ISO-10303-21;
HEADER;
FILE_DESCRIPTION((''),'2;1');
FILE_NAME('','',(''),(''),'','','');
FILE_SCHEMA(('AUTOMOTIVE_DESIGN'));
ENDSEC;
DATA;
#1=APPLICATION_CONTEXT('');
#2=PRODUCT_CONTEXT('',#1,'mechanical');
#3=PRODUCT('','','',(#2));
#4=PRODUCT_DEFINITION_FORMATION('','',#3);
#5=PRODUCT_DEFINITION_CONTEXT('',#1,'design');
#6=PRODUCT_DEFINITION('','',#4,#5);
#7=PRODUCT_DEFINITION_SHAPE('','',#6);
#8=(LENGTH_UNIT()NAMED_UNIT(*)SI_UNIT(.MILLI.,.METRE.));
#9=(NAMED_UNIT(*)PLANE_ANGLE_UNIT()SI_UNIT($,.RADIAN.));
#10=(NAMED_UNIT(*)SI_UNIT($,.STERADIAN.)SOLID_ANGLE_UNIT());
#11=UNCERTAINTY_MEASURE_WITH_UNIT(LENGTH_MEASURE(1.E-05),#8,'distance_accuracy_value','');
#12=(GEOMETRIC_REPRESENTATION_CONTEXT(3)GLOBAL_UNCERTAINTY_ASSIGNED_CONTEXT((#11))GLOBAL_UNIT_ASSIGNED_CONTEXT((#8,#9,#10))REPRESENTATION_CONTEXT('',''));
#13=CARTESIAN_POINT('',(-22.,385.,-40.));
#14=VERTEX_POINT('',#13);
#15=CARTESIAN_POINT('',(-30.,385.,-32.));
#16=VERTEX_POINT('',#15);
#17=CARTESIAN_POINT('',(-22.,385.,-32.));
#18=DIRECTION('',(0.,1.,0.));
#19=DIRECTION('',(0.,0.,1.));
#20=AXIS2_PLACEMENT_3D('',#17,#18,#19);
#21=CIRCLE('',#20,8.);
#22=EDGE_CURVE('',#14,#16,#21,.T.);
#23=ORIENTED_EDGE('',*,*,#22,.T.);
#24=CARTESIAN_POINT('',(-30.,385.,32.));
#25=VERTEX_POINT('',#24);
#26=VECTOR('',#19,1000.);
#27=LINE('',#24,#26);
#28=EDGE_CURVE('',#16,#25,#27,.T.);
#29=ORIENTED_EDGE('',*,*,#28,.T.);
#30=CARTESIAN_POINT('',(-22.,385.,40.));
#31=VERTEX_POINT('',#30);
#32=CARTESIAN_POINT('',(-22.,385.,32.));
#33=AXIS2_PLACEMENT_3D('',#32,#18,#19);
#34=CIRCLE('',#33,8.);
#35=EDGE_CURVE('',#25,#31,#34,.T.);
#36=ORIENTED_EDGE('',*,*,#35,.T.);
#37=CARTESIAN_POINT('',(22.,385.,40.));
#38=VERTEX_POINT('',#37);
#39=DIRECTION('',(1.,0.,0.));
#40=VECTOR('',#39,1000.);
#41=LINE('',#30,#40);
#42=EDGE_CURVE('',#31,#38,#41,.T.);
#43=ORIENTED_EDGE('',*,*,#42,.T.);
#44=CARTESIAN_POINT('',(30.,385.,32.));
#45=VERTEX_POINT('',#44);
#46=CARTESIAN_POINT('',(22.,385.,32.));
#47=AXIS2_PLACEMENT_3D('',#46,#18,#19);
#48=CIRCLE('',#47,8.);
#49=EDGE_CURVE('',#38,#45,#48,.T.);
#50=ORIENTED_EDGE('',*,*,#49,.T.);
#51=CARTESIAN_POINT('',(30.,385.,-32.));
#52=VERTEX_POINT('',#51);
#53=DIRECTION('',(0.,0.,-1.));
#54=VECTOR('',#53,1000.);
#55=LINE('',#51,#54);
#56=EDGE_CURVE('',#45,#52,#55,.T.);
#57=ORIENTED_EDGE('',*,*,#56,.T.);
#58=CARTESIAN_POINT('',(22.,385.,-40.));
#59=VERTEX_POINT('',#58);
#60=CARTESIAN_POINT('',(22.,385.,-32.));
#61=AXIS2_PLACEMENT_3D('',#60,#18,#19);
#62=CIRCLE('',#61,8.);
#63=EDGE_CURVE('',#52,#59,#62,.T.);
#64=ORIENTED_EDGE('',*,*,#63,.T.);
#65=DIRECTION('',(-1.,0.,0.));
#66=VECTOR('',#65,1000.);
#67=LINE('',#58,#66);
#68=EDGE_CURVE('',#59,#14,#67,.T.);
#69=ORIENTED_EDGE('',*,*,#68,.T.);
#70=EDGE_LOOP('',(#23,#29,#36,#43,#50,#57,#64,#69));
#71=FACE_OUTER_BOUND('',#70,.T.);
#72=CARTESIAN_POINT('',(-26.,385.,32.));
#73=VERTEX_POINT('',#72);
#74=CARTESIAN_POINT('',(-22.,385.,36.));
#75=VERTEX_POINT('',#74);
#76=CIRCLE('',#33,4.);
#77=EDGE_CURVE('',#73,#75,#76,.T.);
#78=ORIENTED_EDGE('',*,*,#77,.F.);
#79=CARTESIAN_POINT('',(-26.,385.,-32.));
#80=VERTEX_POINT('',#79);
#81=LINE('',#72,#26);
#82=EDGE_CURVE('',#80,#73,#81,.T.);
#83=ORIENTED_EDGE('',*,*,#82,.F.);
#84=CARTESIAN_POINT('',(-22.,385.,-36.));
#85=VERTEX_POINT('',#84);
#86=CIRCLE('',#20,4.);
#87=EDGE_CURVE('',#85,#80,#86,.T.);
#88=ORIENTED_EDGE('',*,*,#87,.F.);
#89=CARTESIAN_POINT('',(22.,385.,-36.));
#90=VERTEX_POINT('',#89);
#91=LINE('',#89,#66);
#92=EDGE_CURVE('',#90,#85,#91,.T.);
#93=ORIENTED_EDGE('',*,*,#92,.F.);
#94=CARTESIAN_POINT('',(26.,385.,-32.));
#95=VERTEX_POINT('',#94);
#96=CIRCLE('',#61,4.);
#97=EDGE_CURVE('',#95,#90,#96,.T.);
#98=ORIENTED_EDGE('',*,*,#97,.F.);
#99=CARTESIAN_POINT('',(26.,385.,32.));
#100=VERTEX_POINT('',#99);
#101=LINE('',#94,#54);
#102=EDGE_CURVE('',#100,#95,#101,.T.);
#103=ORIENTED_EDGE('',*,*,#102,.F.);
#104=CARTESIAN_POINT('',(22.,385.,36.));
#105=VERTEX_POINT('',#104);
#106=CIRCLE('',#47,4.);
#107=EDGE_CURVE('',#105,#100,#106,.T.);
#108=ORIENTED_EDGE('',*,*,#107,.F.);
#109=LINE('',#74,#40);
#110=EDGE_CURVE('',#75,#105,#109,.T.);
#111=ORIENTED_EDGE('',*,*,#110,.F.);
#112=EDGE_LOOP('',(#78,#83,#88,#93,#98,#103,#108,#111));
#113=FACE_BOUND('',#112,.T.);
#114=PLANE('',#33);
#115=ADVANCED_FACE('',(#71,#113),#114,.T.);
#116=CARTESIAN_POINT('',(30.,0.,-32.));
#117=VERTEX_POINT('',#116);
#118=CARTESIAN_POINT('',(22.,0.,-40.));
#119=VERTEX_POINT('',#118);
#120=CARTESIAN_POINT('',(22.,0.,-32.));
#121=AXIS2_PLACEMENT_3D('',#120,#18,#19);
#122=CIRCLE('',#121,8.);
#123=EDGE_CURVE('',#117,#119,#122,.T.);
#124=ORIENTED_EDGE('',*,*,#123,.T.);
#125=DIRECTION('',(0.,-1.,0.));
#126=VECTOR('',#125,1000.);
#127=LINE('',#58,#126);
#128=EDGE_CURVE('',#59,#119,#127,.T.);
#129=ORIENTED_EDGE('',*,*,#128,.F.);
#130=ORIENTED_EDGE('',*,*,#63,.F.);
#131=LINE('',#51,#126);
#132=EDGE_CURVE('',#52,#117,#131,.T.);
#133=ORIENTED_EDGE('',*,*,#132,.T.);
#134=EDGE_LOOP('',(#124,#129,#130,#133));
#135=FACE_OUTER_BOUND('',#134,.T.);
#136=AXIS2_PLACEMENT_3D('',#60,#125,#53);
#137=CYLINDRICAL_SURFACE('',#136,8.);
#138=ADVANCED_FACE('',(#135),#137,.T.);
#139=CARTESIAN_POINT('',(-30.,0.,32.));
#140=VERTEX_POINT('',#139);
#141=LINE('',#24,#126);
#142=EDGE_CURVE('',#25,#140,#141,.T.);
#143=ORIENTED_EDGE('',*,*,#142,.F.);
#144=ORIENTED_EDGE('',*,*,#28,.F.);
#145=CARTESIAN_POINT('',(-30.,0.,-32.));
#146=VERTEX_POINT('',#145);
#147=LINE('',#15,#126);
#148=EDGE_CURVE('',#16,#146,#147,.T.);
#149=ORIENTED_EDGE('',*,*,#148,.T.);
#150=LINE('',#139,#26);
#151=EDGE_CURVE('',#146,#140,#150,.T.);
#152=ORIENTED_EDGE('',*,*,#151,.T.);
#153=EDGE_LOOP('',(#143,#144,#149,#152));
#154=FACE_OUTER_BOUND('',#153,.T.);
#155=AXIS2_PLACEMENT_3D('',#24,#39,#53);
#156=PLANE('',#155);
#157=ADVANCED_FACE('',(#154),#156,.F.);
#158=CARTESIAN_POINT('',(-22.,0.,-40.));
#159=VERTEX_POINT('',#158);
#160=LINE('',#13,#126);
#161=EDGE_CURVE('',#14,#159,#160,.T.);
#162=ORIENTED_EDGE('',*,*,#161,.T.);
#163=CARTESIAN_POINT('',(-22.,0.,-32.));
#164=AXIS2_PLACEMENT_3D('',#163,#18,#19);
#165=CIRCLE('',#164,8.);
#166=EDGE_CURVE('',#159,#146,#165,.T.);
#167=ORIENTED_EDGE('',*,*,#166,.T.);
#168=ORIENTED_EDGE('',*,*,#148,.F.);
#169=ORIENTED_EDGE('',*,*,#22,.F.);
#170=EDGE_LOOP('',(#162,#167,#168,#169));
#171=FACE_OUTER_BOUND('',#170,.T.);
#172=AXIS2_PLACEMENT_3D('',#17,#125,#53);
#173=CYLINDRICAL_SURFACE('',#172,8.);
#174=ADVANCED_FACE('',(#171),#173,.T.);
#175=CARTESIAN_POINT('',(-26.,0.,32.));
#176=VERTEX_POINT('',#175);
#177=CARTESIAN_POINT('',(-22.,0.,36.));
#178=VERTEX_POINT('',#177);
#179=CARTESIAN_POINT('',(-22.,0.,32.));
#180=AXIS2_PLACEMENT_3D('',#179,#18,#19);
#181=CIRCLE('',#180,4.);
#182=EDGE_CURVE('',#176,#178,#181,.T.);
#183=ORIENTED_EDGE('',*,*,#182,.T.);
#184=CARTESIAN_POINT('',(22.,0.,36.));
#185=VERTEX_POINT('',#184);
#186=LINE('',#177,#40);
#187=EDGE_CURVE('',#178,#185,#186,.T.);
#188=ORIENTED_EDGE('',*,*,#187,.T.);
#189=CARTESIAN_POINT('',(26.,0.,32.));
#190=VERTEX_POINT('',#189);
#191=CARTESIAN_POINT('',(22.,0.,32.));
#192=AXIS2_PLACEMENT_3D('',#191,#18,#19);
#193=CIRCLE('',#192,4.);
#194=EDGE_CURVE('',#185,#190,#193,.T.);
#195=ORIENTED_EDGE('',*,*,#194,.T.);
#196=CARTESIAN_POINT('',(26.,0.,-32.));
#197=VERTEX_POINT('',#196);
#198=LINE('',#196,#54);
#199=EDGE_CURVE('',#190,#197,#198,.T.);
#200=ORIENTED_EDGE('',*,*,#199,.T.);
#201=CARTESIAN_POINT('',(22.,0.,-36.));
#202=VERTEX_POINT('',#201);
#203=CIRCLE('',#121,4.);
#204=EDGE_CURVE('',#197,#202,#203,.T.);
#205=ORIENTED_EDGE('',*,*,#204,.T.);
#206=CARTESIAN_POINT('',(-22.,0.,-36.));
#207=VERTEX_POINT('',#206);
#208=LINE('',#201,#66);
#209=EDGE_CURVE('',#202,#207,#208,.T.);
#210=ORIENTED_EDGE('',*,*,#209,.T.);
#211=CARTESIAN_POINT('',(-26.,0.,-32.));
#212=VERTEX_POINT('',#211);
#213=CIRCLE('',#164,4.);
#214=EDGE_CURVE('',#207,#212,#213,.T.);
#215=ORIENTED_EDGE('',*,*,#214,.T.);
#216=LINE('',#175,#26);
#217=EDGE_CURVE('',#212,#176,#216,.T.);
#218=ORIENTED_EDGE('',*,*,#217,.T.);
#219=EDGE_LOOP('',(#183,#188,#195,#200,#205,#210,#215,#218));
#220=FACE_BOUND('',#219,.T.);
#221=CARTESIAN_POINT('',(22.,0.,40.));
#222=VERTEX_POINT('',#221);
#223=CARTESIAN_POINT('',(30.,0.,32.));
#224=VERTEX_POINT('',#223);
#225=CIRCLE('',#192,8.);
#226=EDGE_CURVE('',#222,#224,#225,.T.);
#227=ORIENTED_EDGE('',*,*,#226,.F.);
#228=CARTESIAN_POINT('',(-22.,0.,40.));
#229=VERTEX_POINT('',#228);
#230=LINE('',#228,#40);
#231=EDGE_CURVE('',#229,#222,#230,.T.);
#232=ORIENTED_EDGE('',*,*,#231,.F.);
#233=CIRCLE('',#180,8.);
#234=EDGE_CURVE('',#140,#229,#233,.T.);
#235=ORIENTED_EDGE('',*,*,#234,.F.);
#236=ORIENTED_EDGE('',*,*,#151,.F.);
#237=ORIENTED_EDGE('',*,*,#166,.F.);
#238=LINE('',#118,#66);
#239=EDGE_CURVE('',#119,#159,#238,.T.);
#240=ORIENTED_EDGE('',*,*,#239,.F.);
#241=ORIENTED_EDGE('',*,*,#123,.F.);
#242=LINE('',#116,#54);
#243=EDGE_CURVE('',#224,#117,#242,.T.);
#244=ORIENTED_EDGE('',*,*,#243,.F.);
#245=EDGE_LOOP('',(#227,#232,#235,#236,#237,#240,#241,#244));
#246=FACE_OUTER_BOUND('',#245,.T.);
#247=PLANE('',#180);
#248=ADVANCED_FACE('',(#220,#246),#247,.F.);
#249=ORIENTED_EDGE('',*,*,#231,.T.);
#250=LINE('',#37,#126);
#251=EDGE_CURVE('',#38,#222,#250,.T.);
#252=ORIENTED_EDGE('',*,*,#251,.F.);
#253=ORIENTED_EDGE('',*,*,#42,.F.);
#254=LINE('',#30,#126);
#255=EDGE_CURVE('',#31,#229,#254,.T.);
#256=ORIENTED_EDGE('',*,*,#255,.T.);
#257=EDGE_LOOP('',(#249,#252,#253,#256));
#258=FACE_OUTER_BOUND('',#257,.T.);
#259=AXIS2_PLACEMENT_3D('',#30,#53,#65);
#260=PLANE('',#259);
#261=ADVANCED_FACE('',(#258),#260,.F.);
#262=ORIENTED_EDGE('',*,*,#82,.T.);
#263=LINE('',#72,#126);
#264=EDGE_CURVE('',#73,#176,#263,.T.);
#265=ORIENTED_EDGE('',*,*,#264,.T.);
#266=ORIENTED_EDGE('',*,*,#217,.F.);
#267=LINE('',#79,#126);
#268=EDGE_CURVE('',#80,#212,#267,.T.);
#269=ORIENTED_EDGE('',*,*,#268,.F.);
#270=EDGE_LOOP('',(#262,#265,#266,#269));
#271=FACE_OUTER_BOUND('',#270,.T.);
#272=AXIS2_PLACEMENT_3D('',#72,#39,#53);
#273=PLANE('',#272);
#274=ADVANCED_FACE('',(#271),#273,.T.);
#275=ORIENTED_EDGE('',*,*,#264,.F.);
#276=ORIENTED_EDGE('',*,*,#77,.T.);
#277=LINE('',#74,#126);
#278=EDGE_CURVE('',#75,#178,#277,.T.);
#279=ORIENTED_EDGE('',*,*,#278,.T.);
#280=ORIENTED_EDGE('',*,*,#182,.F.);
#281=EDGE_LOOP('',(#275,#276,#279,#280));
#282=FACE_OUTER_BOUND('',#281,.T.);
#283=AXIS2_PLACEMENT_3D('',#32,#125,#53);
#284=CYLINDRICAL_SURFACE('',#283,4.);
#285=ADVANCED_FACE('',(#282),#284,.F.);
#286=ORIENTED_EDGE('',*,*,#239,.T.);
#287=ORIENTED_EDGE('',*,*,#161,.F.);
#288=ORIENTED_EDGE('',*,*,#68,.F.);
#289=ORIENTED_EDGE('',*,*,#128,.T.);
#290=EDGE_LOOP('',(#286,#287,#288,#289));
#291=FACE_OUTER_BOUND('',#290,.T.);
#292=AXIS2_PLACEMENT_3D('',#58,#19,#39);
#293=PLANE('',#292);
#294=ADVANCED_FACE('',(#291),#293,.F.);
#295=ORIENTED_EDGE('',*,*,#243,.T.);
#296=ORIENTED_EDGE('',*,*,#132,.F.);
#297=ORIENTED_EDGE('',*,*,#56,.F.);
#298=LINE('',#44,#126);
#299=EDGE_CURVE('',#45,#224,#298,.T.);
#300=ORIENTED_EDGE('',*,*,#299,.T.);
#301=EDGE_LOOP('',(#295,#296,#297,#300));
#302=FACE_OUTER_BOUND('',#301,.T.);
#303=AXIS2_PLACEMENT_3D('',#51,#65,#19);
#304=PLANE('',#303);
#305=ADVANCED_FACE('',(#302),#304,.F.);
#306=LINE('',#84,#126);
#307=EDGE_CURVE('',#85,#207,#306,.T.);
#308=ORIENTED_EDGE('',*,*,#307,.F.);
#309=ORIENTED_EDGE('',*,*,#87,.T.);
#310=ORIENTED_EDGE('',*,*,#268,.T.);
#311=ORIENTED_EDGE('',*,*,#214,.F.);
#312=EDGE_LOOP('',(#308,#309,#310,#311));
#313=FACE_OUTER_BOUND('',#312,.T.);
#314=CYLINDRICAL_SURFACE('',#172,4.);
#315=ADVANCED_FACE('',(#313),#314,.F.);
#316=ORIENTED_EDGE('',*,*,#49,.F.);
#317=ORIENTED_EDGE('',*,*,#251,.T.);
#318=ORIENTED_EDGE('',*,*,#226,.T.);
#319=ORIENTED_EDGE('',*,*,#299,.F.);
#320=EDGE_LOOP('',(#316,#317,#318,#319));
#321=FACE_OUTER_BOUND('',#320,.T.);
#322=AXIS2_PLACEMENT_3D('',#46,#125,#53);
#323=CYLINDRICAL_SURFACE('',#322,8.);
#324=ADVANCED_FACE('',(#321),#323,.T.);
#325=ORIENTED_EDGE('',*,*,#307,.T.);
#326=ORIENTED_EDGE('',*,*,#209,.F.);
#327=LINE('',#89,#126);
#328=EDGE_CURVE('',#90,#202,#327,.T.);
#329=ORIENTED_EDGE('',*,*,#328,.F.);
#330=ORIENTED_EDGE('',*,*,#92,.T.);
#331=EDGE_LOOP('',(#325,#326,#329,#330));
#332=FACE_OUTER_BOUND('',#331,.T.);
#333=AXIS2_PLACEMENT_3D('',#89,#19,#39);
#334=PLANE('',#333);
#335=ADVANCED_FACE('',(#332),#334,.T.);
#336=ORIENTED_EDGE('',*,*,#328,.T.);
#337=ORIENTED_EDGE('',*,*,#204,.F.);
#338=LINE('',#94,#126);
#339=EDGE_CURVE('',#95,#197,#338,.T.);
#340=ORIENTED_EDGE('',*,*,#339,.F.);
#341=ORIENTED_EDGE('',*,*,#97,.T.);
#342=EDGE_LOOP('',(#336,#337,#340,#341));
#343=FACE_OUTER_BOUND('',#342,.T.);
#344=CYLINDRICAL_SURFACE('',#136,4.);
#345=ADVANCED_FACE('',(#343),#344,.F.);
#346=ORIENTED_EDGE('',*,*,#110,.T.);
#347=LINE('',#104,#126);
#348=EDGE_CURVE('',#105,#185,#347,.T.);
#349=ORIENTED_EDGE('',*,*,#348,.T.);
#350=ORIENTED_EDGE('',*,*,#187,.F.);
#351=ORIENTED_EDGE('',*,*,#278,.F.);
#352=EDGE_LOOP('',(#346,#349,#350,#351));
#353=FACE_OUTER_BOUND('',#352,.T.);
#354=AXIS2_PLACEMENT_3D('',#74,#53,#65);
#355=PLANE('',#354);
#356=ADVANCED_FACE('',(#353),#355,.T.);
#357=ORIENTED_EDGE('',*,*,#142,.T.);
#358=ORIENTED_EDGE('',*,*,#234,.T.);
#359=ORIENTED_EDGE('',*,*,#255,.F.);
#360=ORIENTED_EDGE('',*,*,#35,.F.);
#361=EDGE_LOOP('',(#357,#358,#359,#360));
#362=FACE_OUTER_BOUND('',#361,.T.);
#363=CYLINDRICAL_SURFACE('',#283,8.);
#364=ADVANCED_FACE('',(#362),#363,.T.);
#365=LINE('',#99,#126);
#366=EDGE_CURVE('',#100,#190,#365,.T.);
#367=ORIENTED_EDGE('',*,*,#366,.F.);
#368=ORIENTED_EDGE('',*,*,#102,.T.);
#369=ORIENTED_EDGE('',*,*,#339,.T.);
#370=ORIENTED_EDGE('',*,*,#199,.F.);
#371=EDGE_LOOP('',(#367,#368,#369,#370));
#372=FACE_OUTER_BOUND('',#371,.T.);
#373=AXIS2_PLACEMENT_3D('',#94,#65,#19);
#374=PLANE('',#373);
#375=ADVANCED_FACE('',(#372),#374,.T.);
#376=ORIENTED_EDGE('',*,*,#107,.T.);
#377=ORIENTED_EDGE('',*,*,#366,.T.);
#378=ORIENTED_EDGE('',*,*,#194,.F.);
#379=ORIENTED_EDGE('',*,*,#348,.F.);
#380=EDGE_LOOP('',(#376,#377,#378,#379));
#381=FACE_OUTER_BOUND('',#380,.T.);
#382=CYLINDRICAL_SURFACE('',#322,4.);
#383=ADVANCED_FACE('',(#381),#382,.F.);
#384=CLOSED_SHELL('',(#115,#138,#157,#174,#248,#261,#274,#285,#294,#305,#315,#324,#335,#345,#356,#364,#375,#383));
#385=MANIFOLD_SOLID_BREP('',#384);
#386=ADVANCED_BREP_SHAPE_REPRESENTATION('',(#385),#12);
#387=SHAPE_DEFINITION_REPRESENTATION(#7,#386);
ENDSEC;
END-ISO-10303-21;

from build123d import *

# Parameters (mm, degrees)
GB_T_6728_2002_RECTANGULAR_HOLLOW_SECTIO_DEPTH = 385


with BuildPart() as part:
    # Sketch13 → GB/T 6728-2002 rectangular hollow section 80X60X4(1) (new body)
    with BuildSketch(Plane(origin=(0, 0, 0), x_dir=(-1, 0, 0), z_dir=(0, 1, 0))):
        with BuildLine():
            Line((-22, -40), (22, -40))
            ThreePointArc((22, -40), (27.656854249, -37.656854249), (30, -32))
            Line((30, -32), (30, 32))
            ThreePointArc((30, 32), (27.656854249, 37.656854249), (22, 40))
            Line((22, 40), (-22, 40))
            ThreePointArc((-22, 40), (-27.656854249, 37.656854249), (-30, 32))
            Line((-30, 32), (-30, -32))
            ThreePointArc((-30, -32), (-27.656854249, -37.656854249), (-22, -40))
        make_face()
        with BuildLine():
            Line((-22, -36), (22, -36))
            ThreePointArc((22, -36), (24.828427125, -34.828427125), (26, -32))
            Line((26, -32), (26, 32))
            ThreePointArc((26, 32), (24.828427125, 34.828427125), (22, 36))
            Line((22, 36), (-22, 36))
            ThreePointArc((-22, 36), (-24.828427125, 34.828427125), (-26, 32))
            Line((-26, 32), (-26, -32))
            ThreePointArc((-26, -32), (-24.828427125, -34.828427125), (-22, -36))
        make_face(mode=Mode.SUBTRACT)
    extrude(amount=GB_T_6728_2002_RECTANGULAR_HOLLOW_SECTIO_DEPTH)


solid = part.part
